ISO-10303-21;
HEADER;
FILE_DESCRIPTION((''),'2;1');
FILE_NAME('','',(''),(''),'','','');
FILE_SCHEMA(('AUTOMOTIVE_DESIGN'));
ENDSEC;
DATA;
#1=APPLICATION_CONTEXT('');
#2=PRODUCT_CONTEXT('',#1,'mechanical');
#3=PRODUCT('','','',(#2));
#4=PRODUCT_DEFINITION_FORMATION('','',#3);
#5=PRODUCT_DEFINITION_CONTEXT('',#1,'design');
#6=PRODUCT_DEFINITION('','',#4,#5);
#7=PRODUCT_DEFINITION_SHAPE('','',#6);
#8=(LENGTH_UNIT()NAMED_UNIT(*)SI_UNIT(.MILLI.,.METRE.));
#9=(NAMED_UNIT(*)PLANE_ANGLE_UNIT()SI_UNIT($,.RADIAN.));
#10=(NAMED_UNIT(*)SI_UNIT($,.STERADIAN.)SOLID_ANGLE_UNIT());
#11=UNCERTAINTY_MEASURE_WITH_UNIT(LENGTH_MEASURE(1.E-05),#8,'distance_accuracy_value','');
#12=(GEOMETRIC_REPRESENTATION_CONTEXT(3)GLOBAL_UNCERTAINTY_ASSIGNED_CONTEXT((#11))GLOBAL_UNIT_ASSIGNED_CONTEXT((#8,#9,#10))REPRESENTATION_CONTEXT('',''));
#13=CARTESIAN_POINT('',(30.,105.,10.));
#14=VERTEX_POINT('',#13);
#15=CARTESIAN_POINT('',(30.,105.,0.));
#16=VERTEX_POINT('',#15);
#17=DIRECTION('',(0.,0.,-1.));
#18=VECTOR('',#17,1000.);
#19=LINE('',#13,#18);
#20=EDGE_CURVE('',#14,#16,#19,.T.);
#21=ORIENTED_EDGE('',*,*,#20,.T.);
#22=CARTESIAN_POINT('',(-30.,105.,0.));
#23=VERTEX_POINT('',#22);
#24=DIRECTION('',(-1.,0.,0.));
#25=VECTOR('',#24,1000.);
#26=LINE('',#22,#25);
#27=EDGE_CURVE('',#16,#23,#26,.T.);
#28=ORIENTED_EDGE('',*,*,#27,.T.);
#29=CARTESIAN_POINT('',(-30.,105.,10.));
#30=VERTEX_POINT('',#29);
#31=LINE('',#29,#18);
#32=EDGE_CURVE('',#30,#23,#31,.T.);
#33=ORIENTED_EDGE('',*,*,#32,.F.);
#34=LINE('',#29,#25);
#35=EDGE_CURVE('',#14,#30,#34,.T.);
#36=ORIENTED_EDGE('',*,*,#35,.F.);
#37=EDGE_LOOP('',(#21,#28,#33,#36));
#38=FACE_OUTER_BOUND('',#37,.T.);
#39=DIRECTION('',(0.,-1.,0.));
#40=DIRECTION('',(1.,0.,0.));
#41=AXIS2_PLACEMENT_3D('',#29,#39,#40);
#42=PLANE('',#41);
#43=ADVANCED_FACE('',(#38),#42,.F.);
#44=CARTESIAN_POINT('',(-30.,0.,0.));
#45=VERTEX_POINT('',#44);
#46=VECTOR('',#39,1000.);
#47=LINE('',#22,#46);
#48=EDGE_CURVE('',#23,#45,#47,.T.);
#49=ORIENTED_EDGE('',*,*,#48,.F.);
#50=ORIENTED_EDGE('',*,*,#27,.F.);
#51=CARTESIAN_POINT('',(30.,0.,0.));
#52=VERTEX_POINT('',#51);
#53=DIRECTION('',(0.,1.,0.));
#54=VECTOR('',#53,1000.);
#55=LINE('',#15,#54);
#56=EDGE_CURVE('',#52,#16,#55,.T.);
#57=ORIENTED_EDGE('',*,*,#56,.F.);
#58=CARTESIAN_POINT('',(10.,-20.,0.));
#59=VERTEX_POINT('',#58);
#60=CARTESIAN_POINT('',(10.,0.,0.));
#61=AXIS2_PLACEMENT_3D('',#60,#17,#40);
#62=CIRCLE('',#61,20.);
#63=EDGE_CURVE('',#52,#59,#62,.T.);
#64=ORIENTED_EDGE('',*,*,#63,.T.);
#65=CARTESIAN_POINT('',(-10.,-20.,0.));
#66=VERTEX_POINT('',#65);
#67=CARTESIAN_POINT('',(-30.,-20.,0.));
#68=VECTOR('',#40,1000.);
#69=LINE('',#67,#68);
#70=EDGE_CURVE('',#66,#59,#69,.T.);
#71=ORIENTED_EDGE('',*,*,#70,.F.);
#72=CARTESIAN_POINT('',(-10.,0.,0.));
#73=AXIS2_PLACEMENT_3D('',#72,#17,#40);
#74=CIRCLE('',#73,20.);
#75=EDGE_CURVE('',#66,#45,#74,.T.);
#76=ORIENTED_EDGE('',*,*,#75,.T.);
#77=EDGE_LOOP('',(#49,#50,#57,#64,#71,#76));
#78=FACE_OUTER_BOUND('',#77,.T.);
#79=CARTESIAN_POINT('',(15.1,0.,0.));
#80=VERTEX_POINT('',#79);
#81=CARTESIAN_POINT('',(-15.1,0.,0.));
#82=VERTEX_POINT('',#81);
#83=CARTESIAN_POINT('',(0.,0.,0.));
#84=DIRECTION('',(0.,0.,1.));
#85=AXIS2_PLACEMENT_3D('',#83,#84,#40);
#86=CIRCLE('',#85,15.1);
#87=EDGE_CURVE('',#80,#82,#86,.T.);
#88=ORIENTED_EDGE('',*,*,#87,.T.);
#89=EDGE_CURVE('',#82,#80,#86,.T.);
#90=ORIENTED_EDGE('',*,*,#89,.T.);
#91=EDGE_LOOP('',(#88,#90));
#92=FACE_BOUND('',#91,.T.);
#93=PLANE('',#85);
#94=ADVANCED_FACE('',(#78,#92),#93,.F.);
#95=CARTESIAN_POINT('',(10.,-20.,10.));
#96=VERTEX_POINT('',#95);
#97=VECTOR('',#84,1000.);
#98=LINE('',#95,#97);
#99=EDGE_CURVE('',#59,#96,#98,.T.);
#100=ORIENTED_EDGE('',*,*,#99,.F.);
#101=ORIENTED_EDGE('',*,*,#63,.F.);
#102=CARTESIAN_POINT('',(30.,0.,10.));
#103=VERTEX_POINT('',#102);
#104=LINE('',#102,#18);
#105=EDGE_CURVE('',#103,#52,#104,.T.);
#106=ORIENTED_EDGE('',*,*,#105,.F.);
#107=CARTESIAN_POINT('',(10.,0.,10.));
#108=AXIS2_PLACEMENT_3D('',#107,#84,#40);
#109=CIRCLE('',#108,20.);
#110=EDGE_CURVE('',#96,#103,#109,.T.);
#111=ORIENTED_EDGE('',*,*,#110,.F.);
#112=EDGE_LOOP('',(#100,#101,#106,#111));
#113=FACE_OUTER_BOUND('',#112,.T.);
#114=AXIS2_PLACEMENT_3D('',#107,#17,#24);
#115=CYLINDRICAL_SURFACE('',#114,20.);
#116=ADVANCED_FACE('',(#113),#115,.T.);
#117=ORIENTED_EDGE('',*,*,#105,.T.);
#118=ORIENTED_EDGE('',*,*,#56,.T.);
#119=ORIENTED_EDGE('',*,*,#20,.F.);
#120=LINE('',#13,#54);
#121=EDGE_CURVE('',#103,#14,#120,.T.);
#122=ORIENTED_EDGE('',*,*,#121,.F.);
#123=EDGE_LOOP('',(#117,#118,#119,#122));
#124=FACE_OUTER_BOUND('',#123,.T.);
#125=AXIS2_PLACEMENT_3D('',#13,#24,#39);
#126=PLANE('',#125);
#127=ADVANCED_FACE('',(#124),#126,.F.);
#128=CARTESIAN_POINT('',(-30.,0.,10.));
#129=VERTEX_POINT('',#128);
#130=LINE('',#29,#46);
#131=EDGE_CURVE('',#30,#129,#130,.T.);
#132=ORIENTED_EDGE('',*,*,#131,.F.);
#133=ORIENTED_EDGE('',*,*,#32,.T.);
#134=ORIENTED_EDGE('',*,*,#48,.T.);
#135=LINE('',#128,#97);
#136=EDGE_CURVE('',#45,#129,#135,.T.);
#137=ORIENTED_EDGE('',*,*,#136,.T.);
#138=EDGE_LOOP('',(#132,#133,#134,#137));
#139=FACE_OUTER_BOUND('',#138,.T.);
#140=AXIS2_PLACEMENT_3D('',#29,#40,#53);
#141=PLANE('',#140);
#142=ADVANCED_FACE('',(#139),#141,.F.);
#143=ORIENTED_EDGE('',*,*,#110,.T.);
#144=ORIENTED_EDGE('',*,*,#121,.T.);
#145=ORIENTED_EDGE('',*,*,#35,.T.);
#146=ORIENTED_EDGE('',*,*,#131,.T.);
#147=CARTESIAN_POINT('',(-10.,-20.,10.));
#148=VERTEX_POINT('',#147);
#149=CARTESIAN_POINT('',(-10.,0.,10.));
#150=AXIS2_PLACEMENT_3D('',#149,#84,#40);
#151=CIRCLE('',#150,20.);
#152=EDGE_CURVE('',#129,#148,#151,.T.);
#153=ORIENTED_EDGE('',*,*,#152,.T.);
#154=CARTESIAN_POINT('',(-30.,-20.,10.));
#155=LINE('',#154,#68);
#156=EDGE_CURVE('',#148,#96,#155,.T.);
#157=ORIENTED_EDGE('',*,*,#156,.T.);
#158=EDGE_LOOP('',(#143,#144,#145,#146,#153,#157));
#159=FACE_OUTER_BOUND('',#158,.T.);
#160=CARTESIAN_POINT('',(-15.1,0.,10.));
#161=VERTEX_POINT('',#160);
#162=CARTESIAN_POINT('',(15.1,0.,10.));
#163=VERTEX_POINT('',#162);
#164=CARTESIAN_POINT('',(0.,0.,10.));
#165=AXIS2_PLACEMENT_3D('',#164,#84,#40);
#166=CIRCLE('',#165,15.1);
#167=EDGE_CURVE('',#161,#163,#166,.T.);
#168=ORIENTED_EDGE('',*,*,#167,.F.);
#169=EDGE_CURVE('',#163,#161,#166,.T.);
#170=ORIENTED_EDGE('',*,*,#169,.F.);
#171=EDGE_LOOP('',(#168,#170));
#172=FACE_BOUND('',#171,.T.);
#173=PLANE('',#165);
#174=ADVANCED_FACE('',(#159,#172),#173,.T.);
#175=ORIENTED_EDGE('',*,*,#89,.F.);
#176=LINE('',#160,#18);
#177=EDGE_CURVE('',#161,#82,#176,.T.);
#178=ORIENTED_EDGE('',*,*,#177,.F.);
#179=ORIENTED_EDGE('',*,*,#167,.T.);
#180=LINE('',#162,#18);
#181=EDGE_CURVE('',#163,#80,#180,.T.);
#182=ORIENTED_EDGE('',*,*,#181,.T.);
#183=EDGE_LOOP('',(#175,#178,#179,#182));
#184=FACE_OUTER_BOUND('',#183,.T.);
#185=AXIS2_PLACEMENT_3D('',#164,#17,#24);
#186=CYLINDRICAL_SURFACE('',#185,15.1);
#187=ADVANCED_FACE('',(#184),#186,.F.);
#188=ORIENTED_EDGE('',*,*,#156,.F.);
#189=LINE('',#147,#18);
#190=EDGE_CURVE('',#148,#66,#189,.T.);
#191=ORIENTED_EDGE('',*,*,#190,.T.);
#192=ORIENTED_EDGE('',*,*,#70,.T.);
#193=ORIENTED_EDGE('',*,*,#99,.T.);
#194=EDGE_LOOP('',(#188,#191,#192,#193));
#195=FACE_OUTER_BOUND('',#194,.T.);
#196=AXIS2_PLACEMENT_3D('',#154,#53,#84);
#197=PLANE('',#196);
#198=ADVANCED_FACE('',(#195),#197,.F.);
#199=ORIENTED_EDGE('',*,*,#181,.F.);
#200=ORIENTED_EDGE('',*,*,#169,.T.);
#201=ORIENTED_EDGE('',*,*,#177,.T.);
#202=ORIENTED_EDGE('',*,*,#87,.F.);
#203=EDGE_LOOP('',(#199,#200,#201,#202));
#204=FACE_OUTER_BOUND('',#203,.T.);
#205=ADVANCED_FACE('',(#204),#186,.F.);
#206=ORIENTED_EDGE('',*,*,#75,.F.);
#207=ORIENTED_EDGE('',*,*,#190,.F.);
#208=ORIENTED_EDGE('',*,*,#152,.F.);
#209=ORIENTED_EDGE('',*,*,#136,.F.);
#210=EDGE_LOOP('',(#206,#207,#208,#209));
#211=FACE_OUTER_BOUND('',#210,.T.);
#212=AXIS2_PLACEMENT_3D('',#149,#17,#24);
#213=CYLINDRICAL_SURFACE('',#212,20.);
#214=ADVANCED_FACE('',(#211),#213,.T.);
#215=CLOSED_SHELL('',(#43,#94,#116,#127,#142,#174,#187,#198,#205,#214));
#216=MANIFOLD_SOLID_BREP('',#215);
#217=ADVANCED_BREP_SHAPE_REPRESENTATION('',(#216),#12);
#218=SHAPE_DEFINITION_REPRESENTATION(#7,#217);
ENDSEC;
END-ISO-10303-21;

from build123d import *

# Parameters (mm, degrees)
SKETCH_1_W      = 60
SKETCH_1_H      = 125
SKETCH_1_R      = 15.1
EXTRUDE_1_DEPTH = 10
FILLET_1_R      = 20


with BuildPart() as part:
    # 草图1 → 凸台-拉伸1 (new body)
    with BuildSketch(Plane.XY):
        with Locations((0, 42.5)):
            Rectangle(SKETCH_1_W, SKETCH_1_H)
        Circle(SKETCH_1_R, mode=Mode.SUBTRACT)
    extrude(amount=EXTRUDE_1_DEPTH)

    # 圆角1
    fillet_1_edges = [part.edges().sort_by_distance(p)[0] for p in [
        (30, -20, 5),
        (-30, -20, 5),
    ]]
    fillet(fillet_1_edges, radius=FILLET_1_R)


solid = part.part
